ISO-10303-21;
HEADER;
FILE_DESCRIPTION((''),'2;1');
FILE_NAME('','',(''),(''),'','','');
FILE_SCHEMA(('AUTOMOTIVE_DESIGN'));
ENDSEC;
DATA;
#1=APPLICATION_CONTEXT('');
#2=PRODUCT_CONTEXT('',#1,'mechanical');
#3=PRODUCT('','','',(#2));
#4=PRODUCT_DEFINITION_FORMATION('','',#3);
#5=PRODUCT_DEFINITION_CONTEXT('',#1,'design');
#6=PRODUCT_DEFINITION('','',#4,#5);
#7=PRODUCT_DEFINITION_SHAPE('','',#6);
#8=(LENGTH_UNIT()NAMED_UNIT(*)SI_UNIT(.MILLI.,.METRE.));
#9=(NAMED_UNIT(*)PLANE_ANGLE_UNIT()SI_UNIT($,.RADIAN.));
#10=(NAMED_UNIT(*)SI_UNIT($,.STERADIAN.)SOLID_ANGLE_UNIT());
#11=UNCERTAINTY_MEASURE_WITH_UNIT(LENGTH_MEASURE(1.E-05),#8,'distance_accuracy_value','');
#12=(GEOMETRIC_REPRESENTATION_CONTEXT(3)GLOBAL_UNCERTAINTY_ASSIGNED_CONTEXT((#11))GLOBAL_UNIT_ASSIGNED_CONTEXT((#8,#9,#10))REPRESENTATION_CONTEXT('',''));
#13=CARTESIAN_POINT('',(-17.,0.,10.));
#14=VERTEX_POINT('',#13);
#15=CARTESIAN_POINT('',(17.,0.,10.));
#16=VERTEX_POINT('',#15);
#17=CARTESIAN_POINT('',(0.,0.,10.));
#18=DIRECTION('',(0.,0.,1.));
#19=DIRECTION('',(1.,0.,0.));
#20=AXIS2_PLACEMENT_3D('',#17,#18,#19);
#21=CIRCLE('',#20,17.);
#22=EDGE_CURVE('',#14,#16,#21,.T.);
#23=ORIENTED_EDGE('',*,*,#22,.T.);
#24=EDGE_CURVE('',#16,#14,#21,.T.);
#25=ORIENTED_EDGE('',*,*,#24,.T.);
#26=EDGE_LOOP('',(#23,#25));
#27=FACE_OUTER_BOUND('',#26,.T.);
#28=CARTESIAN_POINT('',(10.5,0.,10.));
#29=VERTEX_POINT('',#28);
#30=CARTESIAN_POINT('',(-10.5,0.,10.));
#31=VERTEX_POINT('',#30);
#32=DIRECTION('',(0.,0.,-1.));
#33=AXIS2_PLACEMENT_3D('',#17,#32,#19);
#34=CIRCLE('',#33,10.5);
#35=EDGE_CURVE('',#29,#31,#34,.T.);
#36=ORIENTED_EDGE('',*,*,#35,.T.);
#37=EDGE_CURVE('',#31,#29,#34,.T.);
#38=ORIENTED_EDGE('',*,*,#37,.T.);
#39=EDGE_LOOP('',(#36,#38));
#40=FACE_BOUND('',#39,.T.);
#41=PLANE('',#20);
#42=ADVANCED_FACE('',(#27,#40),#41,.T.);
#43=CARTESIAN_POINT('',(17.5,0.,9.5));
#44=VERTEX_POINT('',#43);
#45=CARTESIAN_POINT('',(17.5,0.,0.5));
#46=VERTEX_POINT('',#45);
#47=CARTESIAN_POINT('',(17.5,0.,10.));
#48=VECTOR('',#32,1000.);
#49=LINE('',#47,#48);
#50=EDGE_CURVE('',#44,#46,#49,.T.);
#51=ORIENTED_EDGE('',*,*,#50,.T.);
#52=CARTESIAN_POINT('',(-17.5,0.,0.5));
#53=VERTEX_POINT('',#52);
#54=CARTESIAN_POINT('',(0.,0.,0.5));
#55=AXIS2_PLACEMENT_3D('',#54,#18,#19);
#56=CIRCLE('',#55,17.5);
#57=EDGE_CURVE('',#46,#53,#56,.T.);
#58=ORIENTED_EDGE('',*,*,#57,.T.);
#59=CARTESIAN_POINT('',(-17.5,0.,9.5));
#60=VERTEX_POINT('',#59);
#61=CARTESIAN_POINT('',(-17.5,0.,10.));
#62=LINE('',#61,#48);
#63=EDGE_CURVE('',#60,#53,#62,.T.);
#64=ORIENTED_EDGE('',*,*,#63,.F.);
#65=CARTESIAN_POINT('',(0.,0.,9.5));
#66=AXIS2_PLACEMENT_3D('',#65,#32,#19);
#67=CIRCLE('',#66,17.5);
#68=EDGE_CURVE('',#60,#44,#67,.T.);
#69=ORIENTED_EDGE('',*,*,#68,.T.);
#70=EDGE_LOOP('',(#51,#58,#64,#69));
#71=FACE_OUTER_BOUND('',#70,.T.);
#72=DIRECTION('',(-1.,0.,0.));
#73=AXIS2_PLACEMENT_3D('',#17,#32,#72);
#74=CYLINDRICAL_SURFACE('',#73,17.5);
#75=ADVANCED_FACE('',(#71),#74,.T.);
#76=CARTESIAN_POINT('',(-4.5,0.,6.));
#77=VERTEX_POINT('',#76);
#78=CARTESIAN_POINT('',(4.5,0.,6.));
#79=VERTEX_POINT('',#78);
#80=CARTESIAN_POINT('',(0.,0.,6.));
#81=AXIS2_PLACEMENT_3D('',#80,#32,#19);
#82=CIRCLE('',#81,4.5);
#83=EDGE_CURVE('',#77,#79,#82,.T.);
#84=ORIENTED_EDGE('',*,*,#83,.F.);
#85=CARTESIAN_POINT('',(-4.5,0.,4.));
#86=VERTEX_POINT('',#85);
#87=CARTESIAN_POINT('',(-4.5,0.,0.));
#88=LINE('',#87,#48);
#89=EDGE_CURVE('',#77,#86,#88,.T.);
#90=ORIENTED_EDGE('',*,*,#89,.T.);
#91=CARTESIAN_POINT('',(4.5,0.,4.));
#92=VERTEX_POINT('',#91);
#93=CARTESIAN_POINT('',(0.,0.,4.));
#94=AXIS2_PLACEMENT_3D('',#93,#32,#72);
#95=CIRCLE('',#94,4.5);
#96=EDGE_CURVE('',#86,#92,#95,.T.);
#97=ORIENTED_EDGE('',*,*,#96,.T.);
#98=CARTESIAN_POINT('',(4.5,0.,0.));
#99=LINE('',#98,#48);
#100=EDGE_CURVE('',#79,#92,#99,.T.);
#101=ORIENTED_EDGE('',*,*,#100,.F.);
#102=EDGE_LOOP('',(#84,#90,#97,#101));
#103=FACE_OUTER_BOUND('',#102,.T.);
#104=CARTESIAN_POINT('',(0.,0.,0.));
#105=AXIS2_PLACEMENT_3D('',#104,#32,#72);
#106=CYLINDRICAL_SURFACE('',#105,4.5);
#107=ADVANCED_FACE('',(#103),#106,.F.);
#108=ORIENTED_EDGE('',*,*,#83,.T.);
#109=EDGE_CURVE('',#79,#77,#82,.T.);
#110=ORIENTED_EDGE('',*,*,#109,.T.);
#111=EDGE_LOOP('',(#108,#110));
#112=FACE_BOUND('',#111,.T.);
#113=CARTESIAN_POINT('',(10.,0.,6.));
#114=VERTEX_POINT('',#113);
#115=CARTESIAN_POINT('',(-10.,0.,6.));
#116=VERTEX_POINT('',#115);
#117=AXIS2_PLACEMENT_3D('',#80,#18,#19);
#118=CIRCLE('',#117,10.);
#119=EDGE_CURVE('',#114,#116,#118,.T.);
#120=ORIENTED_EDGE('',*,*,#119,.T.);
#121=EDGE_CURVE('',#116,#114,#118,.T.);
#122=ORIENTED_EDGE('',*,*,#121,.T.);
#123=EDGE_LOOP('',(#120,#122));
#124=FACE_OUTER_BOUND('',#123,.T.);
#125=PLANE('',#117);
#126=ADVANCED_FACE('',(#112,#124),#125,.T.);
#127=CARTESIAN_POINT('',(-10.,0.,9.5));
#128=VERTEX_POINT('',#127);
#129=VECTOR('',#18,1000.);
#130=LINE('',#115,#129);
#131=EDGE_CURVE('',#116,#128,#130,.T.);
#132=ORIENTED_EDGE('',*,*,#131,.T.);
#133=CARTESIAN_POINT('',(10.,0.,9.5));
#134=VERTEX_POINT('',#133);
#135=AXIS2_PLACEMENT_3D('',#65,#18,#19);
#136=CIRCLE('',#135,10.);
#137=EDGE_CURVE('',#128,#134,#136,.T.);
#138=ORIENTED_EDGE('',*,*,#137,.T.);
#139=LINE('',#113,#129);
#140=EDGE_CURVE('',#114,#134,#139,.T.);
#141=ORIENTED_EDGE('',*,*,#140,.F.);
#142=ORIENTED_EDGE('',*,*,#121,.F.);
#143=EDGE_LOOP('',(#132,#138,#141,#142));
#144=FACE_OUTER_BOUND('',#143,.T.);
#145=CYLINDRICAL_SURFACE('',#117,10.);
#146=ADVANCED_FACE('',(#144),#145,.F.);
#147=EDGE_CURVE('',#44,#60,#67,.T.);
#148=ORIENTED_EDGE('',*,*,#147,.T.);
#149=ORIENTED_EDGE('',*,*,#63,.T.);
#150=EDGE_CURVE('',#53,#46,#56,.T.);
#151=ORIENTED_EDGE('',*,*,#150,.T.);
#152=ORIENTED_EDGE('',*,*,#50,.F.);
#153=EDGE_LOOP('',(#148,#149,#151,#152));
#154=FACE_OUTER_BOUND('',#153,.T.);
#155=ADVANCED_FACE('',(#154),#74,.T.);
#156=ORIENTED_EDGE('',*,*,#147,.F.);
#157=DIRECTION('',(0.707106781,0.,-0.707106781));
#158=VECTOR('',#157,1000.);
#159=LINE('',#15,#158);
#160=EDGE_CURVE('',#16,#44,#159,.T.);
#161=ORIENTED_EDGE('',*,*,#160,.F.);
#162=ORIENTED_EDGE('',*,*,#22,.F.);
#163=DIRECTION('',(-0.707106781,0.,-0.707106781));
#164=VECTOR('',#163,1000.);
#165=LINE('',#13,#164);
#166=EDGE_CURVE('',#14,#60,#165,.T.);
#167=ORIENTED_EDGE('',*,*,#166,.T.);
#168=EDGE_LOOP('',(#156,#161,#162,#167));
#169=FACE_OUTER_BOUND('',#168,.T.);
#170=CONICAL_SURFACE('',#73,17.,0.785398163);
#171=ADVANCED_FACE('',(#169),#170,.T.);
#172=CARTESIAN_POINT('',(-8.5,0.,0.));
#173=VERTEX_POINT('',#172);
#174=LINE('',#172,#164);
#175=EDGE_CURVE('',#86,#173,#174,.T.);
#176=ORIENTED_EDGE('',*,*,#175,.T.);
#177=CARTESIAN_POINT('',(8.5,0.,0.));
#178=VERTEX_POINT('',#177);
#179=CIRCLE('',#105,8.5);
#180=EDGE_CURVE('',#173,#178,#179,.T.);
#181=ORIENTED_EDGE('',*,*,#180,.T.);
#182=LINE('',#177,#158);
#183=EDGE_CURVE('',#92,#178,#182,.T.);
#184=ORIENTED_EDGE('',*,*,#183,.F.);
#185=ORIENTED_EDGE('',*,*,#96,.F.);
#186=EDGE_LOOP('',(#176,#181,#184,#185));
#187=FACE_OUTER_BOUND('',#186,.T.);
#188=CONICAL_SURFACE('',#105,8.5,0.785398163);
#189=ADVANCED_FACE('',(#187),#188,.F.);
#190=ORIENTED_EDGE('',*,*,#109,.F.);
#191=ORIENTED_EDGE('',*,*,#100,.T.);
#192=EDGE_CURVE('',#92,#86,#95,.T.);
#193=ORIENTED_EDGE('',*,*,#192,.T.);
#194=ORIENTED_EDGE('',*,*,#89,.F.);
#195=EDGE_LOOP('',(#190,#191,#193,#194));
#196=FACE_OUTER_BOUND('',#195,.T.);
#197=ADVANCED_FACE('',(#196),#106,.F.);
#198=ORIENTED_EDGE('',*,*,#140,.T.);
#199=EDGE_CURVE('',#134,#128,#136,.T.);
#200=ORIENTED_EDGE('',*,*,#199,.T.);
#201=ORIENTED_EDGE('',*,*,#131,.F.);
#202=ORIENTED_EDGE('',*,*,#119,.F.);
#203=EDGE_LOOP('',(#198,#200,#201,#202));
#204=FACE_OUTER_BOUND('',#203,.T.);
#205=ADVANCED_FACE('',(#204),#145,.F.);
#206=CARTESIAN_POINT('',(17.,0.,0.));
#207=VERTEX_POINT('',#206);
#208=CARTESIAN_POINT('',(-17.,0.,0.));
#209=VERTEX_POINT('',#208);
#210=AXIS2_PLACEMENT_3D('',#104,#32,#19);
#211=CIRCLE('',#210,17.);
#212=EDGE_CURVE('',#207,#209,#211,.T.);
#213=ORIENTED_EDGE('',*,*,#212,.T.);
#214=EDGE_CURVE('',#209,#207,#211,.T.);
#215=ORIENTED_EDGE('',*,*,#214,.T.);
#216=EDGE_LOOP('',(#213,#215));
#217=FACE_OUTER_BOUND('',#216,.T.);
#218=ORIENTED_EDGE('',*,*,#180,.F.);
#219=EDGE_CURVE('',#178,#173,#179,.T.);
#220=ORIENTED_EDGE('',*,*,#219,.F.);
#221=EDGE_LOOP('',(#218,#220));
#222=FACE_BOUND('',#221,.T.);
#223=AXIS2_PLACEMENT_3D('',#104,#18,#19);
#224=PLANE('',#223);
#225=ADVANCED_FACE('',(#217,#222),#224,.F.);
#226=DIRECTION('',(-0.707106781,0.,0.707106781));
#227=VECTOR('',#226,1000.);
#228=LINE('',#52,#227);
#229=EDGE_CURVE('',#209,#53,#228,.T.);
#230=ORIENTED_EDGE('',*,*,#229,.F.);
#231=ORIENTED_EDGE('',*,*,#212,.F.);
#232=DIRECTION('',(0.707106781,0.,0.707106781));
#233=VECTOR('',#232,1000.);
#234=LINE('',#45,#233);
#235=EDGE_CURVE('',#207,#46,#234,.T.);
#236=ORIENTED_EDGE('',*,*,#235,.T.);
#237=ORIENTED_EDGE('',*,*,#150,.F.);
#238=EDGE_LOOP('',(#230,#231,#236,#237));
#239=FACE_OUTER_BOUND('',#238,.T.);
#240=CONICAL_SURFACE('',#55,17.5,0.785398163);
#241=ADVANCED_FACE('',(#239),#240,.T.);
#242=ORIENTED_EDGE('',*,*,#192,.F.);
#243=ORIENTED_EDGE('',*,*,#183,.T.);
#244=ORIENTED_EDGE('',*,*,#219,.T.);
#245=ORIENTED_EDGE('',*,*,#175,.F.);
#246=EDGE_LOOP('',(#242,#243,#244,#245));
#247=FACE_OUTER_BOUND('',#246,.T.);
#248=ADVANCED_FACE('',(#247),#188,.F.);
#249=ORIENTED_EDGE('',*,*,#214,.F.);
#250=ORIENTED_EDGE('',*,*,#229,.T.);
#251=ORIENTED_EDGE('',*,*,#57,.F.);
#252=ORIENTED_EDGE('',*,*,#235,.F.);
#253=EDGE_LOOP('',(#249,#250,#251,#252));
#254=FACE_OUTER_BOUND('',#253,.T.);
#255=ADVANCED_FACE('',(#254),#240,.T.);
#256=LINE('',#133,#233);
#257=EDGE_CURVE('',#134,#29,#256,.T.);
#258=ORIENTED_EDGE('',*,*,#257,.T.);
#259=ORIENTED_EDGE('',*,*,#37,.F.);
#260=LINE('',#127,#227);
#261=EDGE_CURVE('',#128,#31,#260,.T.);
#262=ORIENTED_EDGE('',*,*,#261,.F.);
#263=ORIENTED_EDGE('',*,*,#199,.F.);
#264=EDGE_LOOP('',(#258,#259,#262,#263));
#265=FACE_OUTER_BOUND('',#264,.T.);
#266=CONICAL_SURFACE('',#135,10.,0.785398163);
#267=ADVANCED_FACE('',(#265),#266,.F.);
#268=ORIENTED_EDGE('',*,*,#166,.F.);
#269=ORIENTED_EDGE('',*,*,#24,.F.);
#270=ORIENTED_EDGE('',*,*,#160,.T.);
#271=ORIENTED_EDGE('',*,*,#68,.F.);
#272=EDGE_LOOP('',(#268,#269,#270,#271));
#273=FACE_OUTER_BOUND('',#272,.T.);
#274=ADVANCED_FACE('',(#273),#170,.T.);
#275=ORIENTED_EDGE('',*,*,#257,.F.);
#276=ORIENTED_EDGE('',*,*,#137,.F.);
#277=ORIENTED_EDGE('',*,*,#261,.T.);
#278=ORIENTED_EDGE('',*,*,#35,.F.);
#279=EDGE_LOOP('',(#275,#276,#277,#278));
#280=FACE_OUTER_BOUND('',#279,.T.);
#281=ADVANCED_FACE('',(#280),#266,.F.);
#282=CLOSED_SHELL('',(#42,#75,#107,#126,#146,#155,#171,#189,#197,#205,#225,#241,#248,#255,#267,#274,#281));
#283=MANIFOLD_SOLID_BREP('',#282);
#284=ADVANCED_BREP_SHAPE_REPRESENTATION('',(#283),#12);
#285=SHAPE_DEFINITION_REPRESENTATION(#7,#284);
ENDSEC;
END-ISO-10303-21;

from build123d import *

# Parameters (mm, degrees)
SKETCH1_R                                           = 17.5
BOSS_EXTRUDE1_DEPTH                                 = 10
CHAMFER1_SIZE                                       = 0.5
HOLE_SIZE_PER_SOCKET_FLAT_COUNTEBLZKK_H_D           = 9
HOLE_SIZE_PER_SOCKET_FLAT_COUNTEBLZKK_H_CSINK_D     = 17
HOLE_SIZE_PER_SOCKET_FLAT_COUNTEBLZKK_H_CSINK_ANGLE = 90
SKETCH5_R                                           = 10
CUT_EXTRUDE1_DEPTH                                  = 4
CHAMFER2_SIZE                                       = 0.5


with BuildPart() as part:
    # Sketch1 → Boss-Extrude1 (new body)
    with BuildSketch(Plane.XY):
        Circle(SKETCH1_R)
    extrude(amount=BOSS_EXTRUDE1_DEPTH)

    # Chamfer1
    chamfer1_edges = [part.edges().sort_by_distance(p)[0] for p in [
        (-17.5, 0, 0),
        (-17.5, 0, 10),
    ]]
    chamfer(chamfer1_edges, length=CHAMFER1_SIZE)

    # Hole size (per socket flat counteBLZKk head screw type)1 (through all)
    with Locations(Plane(origin=(0, 0, 0), x_dir=(1, 0, 0), z_dir=(0, 0, -1))):
        with Locations((0, 0)):
            CounterSinkHole(HOLE_SIZE_PER_SOCKET_FLAT_COUNTEBLZKK_H_D / 2, HOLE_SIZE_PER_SOCKET_FLAT_COUNTEBLZKK_H_CSINK_D / 2, counter_sink_angle=HOLE_SIZE_PER_SOCKET_FLAT_COUNTEBLZKK_H_CSINK_ANGLE)

    # Sketch5 → Cut-Extrude1 (cut)
    with BuildSketch(Plane.XY.offset(10)):
        Circle(SKETCH5_R)
    extrude(amount=-CUT_EXTRUDE1_DEPTH, mode=Mode.SUBTRACT)

    # Chamfer2
    chamfer2_edges = [part.edges().sort_by_distance(p)[0] for p in [
        (-10, 0, 10),
    ]]
    chamfer(chamfer2_edges, length=CHAMFER2_SIZE)


solid = part.part
